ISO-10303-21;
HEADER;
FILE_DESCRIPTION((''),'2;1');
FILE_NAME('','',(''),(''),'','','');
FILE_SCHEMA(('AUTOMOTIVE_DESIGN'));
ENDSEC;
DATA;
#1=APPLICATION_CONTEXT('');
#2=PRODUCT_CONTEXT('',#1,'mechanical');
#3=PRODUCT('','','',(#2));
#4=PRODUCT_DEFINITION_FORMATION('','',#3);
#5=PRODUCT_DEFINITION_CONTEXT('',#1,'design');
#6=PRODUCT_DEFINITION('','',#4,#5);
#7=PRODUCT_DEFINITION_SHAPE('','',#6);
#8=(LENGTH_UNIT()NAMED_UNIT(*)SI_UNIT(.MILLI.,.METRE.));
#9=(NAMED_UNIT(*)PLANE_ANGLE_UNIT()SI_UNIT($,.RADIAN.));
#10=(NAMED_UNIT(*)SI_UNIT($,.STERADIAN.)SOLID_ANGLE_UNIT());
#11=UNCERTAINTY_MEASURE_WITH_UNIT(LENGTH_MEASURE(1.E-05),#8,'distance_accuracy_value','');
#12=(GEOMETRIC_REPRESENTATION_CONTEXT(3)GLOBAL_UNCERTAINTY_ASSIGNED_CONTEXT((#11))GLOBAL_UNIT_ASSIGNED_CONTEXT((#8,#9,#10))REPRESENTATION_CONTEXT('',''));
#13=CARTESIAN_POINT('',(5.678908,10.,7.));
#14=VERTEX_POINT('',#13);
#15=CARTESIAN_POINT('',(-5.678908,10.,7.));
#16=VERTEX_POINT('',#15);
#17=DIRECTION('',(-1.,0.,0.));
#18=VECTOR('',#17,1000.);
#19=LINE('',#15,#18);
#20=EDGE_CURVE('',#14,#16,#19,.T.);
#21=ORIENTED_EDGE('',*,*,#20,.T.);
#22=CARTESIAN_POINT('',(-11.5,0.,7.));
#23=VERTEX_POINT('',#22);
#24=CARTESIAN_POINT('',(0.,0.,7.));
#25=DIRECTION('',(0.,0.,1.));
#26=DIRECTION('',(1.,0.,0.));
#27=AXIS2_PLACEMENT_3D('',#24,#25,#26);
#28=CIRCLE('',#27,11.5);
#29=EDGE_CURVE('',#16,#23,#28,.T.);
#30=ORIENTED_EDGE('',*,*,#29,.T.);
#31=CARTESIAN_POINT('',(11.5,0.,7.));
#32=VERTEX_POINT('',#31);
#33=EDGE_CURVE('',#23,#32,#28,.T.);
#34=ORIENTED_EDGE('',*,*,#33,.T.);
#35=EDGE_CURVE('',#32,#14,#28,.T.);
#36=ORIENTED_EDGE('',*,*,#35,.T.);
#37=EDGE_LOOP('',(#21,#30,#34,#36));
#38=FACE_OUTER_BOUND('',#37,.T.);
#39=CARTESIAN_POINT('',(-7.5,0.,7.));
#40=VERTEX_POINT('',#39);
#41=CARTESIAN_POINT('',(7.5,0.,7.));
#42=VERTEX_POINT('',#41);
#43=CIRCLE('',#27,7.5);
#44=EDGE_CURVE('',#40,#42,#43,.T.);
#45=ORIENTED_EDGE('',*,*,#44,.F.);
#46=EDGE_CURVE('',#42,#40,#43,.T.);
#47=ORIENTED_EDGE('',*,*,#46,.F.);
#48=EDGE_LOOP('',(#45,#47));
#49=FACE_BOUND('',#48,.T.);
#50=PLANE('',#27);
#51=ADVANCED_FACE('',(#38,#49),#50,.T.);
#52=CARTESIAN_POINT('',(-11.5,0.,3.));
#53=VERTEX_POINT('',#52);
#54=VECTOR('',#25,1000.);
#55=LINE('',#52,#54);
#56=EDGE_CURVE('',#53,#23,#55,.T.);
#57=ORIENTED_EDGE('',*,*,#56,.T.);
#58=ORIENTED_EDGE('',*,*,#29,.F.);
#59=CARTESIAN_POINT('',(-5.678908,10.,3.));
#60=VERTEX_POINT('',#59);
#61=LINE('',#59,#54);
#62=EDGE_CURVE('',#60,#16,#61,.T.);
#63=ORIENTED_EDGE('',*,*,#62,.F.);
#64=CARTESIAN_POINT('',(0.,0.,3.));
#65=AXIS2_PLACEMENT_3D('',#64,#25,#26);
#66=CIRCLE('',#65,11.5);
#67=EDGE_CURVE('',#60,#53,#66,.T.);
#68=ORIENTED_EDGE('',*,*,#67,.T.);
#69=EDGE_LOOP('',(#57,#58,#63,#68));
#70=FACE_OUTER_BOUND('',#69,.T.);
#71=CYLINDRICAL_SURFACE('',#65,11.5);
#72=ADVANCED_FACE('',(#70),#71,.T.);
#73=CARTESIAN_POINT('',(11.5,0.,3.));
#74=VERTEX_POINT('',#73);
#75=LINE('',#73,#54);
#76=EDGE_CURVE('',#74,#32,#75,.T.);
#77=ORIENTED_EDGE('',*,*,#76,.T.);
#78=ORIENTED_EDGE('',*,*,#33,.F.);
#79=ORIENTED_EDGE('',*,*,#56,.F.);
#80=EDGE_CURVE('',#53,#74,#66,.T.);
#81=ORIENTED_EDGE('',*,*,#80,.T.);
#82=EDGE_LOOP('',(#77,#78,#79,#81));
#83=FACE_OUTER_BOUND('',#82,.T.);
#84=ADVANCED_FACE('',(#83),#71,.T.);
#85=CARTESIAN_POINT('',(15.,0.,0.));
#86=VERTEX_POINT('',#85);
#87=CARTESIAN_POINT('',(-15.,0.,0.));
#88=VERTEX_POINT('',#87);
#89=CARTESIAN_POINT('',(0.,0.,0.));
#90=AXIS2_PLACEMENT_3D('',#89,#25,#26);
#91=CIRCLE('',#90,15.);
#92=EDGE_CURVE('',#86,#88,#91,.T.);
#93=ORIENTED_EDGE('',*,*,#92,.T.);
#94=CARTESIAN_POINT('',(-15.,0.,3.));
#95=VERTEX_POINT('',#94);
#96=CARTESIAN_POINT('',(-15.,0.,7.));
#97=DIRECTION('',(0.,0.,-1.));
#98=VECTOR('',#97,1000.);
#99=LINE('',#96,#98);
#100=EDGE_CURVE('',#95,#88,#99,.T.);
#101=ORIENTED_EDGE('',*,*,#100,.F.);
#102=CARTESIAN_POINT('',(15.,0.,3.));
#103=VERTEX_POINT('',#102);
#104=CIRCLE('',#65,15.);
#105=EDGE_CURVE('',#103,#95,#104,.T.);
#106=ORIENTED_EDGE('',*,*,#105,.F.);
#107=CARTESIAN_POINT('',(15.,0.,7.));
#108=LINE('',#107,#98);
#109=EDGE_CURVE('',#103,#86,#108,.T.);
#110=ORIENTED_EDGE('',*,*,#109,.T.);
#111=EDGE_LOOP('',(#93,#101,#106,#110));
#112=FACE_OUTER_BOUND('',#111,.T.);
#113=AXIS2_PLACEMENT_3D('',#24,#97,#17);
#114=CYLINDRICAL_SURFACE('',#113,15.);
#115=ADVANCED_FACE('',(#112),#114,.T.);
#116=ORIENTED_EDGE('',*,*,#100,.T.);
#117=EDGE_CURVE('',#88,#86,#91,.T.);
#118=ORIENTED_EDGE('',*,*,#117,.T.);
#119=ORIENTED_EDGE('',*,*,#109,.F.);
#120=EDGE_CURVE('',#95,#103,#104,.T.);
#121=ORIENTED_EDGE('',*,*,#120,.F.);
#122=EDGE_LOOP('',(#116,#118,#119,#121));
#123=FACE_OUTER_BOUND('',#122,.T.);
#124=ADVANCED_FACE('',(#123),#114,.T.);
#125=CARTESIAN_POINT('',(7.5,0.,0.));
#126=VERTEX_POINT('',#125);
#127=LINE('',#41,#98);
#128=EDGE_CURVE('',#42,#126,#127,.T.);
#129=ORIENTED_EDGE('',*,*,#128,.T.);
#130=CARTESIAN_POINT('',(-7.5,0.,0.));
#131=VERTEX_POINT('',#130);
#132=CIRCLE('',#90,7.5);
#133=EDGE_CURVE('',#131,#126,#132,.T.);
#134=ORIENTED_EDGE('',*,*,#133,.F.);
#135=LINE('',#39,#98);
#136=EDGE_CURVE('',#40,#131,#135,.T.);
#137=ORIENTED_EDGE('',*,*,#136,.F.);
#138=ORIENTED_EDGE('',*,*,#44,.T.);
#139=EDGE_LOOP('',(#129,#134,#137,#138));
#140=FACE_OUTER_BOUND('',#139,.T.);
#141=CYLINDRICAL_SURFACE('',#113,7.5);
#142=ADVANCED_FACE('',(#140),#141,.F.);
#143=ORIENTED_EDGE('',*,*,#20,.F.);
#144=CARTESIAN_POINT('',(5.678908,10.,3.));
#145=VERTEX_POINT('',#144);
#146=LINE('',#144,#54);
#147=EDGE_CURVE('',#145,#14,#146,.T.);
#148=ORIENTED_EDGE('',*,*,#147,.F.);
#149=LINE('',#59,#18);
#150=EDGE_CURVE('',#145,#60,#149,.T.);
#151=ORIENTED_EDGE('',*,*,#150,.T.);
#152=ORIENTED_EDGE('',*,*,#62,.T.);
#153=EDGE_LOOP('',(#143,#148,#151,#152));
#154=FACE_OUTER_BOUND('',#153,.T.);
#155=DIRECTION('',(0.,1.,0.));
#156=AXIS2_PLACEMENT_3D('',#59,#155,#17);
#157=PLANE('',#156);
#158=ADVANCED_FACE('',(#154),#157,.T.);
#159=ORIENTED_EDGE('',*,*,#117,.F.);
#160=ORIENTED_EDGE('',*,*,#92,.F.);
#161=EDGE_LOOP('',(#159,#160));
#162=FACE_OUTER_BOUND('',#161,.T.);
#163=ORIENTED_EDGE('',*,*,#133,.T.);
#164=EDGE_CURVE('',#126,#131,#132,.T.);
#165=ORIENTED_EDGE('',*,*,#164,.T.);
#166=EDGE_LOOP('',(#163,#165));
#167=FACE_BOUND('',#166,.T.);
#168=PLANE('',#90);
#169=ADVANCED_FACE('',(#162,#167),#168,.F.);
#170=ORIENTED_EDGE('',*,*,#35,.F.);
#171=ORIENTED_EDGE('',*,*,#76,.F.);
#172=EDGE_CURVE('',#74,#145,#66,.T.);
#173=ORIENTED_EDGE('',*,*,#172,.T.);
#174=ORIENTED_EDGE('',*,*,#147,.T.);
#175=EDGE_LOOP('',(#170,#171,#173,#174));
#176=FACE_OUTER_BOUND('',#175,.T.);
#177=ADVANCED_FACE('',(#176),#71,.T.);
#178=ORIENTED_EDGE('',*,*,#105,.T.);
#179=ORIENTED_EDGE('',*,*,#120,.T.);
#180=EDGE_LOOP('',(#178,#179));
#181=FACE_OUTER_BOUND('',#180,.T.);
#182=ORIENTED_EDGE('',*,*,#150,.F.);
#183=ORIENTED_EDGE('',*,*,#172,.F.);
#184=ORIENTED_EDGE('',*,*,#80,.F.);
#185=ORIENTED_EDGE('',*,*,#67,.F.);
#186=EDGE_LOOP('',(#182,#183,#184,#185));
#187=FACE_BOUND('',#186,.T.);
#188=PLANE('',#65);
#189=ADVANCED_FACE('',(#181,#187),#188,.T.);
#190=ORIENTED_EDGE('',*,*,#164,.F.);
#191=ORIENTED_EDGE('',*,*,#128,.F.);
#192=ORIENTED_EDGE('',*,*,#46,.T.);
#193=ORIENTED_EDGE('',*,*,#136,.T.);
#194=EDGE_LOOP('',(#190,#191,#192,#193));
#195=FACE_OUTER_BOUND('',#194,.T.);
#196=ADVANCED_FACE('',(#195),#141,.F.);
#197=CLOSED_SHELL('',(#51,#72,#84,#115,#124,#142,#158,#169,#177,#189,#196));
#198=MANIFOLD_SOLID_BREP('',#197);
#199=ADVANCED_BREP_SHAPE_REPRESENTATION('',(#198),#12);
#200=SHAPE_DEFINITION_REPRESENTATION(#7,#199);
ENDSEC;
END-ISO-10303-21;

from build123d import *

# Parameters (mm, degrees)
SKETCH_1_R          = 15
SKETCH_1_R_2        = 7.5
EXTRUDE_1_DEPTH     = 7
CUT_EXTRUDE_START   = -4
SKETCH_2_R          = 15
CUT_EXTRUDE_2_DEPTH = 4


with BuildPart() as part:
    # 草图1 → 凸台-拉伸1 (new body)
    with BuildSketch(Plane.XY):
        Circle(SKETCH_1_R)
        Circle(SKETCH_1_R_2, mode=Mode.SUBTRACT)
    extrude(amount=EXTRUDE_1_DEPTH)

    # 草图2 → 切除-拉伸2 (cut)
    with BuildSketch(Plane.XY.offset(7).offset(CUT_EXTRUDE_START)):
        Circle(SKETCH_2_R)
        with BuildLine():
            Line((-5.678908346, 10), (5.678908346, 10))
            ThreePointArc((5.678908346, 10), (0, -11.5), (-5.678908346, 10))
        make_face(mode=Mode.SUBTRACT)
    extrude(amount=CUT_EXTRUDE_2_DEPTH, mode=Mode.SUBTRACT)


solid = part.part
